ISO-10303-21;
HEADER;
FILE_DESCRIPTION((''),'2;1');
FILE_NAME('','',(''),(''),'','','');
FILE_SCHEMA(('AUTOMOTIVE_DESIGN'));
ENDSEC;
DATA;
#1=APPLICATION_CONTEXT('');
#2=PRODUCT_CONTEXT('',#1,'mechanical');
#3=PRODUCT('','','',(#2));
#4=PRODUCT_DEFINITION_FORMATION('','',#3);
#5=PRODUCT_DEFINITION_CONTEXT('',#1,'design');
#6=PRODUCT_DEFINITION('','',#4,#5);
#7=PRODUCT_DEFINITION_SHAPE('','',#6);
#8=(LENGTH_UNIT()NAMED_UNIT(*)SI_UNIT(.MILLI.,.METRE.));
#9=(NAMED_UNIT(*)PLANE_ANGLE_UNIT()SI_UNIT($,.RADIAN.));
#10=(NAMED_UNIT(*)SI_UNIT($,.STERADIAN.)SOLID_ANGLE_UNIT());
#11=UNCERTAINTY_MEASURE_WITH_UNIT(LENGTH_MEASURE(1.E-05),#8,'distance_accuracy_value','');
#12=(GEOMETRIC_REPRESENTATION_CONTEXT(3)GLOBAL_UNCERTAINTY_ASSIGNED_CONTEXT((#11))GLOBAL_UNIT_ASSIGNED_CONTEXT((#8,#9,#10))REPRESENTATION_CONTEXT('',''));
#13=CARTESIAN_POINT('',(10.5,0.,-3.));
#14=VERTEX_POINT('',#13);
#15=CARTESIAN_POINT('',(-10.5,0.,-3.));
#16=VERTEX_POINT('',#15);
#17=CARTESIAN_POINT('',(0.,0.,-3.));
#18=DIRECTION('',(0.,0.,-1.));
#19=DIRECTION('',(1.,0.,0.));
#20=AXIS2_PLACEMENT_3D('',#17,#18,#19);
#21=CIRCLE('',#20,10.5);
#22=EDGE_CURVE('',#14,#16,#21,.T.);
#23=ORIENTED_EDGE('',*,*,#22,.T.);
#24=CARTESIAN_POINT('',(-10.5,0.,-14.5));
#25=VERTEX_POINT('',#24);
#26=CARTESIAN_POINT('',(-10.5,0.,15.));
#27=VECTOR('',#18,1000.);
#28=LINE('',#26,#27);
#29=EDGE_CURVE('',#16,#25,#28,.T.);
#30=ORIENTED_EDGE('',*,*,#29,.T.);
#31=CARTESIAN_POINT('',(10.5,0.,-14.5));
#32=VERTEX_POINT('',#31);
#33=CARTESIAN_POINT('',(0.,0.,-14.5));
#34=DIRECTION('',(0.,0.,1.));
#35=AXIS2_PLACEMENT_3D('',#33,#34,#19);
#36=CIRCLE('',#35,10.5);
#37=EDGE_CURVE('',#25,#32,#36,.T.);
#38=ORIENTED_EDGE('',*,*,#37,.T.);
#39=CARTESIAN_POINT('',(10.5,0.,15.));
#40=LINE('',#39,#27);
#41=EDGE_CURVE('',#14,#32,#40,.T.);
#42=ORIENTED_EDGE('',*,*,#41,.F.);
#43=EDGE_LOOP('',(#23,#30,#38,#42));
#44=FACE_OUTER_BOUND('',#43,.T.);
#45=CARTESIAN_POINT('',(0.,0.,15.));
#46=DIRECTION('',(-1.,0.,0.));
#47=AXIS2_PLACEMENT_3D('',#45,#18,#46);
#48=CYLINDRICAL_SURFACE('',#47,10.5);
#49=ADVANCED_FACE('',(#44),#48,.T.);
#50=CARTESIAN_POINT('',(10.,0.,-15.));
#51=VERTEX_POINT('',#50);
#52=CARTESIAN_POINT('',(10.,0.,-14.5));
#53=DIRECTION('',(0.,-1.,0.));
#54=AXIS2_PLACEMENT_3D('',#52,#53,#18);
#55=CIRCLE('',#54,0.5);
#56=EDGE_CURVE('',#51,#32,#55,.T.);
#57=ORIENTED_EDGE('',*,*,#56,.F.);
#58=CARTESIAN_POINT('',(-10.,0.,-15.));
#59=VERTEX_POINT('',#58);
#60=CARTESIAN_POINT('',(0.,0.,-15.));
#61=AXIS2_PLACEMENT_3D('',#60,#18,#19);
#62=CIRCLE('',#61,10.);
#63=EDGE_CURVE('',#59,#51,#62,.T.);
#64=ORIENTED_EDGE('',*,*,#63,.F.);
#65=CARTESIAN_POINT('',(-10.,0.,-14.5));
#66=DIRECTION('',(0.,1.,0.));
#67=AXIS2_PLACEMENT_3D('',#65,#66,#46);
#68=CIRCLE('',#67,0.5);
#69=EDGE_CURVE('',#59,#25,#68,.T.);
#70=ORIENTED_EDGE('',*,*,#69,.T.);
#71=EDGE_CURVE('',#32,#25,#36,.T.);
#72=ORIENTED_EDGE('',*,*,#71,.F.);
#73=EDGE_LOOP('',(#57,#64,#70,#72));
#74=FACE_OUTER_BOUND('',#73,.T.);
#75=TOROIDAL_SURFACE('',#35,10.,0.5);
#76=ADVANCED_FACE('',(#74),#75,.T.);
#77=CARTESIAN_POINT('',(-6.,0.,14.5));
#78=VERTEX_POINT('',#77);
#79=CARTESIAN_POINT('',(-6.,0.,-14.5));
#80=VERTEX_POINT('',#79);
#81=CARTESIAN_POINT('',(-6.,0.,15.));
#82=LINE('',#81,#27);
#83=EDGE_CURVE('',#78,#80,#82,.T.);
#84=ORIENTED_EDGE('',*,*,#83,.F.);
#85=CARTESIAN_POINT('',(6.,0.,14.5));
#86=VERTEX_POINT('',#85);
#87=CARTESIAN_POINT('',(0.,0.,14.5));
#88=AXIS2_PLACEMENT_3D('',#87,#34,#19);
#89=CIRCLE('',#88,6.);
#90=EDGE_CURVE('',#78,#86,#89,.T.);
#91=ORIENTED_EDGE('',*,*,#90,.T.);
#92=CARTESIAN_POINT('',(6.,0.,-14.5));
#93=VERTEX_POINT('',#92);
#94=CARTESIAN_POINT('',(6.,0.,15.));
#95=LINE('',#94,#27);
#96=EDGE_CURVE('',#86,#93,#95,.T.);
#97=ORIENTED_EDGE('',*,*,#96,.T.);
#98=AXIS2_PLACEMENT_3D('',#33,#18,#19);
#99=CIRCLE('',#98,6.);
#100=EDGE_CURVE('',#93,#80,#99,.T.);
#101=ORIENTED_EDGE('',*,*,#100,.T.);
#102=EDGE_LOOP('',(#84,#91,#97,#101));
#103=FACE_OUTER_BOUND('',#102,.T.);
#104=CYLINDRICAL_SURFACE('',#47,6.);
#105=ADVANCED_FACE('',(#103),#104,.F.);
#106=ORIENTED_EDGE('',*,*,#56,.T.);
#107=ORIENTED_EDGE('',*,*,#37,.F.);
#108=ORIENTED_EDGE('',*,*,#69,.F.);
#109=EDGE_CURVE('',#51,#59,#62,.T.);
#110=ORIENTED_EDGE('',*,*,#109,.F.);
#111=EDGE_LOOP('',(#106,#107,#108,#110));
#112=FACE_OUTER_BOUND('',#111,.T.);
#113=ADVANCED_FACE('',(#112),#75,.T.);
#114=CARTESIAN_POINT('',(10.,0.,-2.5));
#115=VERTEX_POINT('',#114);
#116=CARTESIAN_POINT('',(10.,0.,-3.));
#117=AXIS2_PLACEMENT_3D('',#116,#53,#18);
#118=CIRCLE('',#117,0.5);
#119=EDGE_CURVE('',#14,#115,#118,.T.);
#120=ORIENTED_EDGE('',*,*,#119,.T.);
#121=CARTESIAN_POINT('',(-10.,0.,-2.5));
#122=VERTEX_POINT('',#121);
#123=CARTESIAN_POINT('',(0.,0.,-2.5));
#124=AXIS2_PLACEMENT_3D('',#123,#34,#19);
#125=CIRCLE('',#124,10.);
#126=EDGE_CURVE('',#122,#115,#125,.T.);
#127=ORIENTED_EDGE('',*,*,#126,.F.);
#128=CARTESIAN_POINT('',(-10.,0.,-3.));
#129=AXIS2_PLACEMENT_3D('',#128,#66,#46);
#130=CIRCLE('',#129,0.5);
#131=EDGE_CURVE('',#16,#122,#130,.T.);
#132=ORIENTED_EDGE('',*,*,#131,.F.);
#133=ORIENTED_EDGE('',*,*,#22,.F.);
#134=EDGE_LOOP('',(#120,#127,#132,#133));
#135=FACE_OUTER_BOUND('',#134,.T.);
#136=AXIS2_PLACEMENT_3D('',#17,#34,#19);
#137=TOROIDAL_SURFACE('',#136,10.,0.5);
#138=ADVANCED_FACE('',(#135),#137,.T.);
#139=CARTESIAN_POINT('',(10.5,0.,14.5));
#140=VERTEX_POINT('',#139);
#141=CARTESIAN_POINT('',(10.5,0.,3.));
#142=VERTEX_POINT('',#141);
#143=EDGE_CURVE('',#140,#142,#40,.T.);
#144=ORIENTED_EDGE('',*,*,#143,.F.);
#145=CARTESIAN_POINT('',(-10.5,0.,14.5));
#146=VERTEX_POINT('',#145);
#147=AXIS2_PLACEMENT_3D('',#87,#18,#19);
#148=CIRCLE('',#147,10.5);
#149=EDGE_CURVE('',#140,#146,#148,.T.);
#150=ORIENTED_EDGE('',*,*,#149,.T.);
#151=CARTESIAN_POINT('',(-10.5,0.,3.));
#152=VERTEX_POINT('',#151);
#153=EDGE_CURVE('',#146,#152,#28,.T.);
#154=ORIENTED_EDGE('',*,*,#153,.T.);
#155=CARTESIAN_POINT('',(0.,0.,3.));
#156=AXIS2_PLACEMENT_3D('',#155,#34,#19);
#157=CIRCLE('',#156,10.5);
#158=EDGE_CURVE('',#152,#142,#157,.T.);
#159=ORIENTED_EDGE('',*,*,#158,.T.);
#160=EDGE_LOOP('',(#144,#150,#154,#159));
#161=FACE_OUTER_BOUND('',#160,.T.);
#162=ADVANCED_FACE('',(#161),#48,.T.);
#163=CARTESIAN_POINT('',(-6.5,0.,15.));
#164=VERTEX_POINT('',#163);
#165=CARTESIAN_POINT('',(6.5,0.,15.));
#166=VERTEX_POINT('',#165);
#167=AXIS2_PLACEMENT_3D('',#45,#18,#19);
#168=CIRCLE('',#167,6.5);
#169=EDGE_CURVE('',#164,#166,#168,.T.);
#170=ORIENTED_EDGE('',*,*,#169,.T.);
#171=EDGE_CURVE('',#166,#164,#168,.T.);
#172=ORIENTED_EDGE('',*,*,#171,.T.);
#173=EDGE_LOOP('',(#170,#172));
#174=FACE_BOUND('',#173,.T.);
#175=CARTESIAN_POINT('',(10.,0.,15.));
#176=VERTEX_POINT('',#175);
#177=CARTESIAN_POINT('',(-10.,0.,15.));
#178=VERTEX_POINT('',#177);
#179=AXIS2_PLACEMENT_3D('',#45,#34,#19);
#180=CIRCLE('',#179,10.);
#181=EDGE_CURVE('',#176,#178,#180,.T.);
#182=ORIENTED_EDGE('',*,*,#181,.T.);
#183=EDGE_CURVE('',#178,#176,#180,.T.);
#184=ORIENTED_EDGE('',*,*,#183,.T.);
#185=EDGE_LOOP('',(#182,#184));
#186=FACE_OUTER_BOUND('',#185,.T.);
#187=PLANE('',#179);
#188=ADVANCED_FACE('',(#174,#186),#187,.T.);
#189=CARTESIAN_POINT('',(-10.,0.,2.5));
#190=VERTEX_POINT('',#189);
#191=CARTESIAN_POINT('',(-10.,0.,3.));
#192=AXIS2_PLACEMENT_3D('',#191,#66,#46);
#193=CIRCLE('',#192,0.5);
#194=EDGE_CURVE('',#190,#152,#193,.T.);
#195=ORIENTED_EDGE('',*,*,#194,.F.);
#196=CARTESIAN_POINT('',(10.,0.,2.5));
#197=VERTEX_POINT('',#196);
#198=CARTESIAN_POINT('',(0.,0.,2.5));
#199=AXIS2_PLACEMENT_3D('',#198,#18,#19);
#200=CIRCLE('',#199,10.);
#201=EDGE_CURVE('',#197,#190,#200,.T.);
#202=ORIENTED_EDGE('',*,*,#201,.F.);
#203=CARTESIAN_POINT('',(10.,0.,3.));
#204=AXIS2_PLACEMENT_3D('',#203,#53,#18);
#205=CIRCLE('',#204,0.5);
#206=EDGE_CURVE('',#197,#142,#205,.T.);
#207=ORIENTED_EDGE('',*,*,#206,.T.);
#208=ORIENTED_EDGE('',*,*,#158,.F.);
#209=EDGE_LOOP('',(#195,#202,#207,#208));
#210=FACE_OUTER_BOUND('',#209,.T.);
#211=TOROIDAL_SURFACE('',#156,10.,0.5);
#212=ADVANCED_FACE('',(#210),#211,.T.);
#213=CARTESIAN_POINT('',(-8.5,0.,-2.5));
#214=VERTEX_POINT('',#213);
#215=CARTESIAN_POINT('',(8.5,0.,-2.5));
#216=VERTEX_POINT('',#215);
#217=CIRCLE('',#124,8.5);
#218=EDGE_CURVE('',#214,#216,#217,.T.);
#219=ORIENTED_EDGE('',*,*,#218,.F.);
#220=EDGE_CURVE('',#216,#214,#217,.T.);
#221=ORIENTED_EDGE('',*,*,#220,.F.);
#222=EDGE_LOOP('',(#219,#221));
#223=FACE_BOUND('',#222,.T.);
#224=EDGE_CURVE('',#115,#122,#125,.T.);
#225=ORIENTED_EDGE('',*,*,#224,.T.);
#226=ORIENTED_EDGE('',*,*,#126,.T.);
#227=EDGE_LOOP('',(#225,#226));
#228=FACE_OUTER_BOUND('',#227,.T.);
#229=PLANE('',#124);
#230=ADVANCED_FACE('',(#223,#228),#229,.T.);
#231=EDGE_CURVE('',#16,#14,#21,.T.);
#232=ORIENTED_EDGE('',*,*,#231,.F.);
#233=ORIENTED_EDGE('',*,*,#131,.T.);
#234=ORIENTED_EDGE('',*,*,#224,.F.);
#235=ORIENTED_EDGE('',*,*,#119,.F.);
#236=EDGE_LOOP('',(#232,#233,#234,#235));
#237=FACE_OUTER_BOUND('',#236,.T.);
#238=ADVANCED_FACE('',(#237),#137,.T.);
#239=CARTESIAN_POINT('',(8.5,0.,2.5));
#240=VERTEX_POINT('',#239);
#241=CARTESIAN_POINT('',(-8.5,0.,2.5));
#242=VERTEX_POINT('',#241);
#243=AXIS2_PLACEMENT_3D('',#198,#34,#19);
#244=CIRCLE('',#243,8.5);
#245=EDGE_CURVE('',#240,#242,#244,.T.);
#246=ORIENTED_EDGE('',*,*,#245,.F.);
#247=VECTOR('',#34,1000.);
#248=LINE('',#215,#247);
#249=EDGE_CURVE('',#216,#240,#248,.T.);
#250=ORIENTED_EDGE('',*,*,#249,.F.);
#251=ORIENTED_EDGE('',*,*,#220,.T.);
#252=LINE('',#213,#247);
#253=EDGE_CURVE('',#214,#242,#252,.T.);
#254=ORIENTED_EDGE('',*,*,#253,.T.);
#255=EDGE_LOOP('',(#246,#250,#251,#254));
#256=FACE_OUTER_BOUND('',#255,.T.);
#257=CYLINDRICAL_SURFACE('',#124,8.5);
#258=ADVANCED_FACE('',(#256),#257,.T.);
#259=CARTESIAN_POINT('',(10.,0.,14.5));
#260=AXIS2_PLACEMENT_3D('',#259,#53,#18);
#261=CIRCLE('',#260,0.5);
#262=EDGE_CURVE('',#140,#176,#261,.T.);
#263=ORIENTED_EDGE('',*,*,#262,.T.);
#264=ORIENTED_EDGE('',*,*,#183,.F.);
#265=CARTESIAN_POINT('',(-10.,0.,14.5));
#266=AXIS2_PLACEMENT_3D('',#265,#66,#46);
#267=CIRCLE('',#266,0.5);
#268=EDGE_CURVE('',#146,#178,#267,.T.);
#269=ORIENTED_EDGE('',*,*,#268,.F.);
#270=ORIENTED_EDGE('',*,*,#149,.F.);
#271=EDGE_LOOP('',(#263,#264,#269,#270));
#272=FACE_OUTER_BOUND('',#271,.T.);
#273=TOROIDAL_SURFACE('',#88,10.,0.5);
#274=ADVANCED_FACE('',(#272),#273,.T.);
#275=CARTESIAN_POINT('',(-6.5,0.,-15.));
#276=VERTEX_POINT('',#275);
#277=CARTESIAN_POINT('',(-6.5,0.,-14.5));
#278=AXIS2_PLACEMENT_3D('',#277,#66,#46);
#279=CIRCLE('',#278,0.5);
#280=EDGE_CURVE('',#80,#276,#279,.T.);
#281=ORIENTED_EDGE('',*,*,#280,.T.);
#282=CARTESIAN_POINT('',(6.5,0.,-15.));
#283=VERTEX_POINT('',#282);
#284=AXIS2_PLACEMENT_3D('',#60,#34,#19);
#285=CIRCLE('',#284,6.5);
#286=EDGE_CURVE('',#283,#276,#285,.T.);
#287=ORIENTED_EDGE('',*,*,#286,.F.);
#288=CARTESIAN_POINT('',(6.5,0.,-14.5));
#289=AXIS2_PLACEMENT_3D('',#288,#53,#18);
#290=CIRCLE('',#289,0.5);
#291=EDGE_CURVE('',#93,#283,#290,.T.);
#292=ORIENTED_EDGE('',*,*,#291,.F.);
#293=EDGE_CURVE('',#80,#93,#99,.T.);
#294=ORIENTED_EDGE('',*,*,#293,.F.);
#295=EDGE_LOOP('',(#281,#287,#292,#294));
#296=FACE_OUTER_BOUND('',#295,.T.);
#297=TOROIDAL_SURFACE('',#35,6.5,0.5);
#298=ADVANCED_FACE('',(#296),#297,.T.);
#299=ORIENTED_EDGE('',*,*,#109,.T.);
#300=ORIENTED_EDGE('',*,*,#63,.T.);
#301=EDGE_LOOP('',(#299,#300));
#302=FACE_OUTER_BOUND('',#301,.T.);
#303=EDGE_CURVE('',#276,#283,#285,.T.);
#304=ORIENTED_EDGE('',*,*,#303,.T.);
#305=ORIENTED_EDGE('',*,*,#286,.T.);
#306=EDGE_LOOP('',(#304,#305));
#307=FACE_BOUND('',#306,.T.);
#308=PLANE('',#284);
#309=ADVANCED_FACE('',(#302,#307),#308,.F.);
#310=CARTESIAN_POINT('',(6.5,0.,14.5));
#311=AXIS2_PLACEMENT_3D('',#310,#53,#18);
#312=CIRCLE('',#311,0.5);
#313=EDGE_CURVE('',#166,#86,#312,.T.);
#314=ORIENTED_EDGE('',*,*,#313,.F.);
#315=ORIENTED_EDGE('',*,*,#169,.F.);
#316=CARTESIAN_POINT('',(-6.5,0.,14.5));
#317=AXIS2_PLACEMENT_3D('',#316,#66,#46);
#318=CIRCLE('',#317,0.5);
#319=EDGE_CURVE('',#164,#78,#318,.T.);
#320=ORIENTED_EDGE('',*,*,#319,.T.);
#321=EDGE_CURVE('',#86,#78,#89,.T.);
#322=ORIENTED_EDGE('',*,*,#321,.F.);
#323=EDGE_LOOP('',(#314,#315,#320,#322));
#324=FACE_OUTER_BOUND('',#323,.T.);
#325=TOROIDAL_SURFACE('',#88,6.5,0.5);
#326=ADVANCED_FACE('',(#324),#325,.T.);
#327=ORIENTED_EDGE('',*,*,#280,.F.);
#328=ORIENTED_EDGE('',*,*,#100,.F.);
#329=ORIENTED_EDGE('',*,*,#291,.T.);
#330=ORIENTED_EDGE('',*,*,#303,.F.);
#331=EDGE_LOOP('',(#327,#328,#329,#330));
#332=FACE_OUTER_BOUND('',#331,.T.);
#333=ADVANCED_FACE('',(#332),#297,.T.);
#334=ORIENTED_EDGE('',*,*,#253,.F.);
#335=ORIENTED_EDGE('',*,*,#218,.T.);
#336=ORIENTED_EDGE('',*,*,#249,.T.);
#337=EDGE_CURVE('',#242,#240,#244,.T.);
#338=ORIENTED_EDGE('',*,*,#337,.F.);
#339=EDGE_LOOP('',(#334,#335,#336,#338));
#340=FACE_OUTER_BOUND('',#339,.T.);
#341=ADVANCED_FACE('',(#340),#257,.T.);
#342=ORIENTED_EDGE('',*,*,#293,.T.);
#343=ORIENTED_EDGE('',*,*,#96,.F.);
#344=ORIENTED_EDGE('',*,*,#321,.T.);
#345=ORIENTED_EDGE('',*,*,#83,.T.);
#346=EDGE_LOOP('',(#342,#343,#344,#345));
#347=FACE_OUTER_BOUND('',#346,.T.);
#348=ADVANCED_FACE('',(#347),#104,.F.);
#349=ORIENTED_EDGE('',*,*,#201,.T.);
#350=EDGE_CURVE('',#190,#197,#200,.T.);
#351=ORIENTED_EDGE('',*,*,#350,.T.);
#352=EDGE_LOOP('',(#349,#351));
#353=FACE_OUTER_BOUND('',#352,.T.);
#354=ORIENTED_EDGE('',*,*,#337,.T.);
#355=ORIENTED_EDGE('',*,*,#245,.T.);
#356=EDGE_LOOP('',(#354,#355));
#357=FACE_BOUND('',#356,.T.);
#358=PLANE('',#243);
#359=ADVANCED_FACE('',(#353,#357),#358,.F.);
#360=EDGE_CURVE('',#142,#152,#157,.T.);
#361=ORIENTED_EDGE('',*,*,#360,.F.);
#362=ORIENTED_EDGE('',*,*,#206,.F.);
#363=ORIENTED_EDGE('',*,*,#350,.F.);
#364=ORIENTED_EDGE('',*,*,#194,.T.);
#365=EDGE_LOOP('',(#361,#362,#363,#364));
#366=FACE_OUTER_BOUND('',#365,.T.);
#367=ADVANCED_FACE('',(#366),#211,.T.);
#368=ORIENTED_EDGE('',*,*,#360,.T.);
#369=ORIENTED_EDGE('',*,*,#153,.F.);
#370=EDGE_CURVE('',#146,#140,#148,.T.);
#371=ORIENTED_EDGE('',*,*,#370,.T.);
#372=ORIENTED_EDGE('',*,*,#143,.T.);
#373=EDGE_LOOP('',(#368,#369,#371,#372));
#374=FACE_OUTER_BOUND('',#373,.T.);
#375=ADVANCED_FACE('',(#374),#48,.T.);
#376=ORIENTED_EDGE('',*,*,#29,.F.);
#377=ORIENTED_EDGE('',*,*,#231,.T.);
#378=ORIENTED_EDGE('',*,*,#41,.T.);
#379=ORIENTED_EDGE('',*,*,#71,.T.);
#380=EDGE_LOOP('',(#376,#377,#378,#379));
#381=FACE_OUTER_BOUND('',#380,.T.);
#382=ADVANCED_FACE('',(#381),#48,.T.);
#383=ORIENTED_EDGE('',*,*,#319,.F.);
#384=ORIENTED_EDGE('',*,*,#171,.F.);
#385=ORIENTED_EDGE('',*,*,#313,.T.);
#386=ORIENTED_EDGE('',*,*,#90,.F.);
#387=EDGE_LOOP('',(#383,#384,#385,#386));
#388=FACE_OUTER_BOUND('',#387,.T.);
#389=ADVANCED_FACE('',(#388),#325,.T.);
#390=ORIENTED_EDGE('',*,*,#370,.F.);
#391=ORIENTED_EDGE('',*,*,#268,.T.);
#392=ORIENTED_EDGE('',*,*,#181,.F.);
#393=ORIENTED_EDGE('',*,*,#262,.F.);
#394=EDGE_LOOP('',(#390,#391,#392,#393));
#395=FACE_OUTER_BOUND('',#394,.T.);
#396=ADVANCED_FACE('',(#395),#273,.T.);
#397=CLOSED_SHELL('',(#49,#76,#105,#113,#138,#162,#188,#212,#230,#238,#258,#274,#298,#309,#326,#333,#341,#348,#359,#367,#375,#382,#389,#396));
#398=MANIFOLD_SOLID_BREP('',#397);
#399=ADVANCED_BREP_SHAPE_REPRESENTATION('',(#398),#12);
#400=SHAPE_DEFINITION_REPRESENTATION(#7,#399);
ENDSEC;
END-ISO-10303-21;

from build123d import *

# Parameters (mm, degrees)
SKETCH1_R           = 10.5
SKETCH1_R_2         = 6
BOSS_EXTRUDE1_DEPTH = 15
SKETCH2_R           = 14.113260249
SKETCH2_R_2         = 8.5
CUT_EXTRUDE1_DEPTH  = 2.5
FILLET1_R           = 0.5


with BuildPart() as part:
    # Sketch1 → Boss-Extrude1 (new, symmetric)
    with BuildSketch(Plane.XY):
        Circle(SKETCH1_R)
        Circle(SKETCH1_R_2, mode=Mode.SUBTRACT)
    extrude(amount=BOSS_EXTRUDE1_DEPTH, both=True)

    # Sketch2 → Cut-Extrude1 (cut, symmetric)
    with BuildSketch(Plane.XY):
        Circle(SKETCH2_R)
        Circle(SKETCH2_R_2, mode=Mode.SUBTRACT)
    extrude(amount=CUT_EXTRUDE1_DEPTH, both=True, mode=Mode.SUBTRACT)

    # Fillet1
    fillet1_edges = [part.edges().sort_by_distance(p)[0] for p in [
        (-10.5, 0, 2.5),
        (-10.5, 0, -2.5),
        (-10.5, 0, -15),
        (-10.5, 0, 15),
        (-6, 0, -15),
        (-6, 0, 15),
    ]]
    fillet(fillet1_edges, radius=FILLET1_R)


solid = part.part
